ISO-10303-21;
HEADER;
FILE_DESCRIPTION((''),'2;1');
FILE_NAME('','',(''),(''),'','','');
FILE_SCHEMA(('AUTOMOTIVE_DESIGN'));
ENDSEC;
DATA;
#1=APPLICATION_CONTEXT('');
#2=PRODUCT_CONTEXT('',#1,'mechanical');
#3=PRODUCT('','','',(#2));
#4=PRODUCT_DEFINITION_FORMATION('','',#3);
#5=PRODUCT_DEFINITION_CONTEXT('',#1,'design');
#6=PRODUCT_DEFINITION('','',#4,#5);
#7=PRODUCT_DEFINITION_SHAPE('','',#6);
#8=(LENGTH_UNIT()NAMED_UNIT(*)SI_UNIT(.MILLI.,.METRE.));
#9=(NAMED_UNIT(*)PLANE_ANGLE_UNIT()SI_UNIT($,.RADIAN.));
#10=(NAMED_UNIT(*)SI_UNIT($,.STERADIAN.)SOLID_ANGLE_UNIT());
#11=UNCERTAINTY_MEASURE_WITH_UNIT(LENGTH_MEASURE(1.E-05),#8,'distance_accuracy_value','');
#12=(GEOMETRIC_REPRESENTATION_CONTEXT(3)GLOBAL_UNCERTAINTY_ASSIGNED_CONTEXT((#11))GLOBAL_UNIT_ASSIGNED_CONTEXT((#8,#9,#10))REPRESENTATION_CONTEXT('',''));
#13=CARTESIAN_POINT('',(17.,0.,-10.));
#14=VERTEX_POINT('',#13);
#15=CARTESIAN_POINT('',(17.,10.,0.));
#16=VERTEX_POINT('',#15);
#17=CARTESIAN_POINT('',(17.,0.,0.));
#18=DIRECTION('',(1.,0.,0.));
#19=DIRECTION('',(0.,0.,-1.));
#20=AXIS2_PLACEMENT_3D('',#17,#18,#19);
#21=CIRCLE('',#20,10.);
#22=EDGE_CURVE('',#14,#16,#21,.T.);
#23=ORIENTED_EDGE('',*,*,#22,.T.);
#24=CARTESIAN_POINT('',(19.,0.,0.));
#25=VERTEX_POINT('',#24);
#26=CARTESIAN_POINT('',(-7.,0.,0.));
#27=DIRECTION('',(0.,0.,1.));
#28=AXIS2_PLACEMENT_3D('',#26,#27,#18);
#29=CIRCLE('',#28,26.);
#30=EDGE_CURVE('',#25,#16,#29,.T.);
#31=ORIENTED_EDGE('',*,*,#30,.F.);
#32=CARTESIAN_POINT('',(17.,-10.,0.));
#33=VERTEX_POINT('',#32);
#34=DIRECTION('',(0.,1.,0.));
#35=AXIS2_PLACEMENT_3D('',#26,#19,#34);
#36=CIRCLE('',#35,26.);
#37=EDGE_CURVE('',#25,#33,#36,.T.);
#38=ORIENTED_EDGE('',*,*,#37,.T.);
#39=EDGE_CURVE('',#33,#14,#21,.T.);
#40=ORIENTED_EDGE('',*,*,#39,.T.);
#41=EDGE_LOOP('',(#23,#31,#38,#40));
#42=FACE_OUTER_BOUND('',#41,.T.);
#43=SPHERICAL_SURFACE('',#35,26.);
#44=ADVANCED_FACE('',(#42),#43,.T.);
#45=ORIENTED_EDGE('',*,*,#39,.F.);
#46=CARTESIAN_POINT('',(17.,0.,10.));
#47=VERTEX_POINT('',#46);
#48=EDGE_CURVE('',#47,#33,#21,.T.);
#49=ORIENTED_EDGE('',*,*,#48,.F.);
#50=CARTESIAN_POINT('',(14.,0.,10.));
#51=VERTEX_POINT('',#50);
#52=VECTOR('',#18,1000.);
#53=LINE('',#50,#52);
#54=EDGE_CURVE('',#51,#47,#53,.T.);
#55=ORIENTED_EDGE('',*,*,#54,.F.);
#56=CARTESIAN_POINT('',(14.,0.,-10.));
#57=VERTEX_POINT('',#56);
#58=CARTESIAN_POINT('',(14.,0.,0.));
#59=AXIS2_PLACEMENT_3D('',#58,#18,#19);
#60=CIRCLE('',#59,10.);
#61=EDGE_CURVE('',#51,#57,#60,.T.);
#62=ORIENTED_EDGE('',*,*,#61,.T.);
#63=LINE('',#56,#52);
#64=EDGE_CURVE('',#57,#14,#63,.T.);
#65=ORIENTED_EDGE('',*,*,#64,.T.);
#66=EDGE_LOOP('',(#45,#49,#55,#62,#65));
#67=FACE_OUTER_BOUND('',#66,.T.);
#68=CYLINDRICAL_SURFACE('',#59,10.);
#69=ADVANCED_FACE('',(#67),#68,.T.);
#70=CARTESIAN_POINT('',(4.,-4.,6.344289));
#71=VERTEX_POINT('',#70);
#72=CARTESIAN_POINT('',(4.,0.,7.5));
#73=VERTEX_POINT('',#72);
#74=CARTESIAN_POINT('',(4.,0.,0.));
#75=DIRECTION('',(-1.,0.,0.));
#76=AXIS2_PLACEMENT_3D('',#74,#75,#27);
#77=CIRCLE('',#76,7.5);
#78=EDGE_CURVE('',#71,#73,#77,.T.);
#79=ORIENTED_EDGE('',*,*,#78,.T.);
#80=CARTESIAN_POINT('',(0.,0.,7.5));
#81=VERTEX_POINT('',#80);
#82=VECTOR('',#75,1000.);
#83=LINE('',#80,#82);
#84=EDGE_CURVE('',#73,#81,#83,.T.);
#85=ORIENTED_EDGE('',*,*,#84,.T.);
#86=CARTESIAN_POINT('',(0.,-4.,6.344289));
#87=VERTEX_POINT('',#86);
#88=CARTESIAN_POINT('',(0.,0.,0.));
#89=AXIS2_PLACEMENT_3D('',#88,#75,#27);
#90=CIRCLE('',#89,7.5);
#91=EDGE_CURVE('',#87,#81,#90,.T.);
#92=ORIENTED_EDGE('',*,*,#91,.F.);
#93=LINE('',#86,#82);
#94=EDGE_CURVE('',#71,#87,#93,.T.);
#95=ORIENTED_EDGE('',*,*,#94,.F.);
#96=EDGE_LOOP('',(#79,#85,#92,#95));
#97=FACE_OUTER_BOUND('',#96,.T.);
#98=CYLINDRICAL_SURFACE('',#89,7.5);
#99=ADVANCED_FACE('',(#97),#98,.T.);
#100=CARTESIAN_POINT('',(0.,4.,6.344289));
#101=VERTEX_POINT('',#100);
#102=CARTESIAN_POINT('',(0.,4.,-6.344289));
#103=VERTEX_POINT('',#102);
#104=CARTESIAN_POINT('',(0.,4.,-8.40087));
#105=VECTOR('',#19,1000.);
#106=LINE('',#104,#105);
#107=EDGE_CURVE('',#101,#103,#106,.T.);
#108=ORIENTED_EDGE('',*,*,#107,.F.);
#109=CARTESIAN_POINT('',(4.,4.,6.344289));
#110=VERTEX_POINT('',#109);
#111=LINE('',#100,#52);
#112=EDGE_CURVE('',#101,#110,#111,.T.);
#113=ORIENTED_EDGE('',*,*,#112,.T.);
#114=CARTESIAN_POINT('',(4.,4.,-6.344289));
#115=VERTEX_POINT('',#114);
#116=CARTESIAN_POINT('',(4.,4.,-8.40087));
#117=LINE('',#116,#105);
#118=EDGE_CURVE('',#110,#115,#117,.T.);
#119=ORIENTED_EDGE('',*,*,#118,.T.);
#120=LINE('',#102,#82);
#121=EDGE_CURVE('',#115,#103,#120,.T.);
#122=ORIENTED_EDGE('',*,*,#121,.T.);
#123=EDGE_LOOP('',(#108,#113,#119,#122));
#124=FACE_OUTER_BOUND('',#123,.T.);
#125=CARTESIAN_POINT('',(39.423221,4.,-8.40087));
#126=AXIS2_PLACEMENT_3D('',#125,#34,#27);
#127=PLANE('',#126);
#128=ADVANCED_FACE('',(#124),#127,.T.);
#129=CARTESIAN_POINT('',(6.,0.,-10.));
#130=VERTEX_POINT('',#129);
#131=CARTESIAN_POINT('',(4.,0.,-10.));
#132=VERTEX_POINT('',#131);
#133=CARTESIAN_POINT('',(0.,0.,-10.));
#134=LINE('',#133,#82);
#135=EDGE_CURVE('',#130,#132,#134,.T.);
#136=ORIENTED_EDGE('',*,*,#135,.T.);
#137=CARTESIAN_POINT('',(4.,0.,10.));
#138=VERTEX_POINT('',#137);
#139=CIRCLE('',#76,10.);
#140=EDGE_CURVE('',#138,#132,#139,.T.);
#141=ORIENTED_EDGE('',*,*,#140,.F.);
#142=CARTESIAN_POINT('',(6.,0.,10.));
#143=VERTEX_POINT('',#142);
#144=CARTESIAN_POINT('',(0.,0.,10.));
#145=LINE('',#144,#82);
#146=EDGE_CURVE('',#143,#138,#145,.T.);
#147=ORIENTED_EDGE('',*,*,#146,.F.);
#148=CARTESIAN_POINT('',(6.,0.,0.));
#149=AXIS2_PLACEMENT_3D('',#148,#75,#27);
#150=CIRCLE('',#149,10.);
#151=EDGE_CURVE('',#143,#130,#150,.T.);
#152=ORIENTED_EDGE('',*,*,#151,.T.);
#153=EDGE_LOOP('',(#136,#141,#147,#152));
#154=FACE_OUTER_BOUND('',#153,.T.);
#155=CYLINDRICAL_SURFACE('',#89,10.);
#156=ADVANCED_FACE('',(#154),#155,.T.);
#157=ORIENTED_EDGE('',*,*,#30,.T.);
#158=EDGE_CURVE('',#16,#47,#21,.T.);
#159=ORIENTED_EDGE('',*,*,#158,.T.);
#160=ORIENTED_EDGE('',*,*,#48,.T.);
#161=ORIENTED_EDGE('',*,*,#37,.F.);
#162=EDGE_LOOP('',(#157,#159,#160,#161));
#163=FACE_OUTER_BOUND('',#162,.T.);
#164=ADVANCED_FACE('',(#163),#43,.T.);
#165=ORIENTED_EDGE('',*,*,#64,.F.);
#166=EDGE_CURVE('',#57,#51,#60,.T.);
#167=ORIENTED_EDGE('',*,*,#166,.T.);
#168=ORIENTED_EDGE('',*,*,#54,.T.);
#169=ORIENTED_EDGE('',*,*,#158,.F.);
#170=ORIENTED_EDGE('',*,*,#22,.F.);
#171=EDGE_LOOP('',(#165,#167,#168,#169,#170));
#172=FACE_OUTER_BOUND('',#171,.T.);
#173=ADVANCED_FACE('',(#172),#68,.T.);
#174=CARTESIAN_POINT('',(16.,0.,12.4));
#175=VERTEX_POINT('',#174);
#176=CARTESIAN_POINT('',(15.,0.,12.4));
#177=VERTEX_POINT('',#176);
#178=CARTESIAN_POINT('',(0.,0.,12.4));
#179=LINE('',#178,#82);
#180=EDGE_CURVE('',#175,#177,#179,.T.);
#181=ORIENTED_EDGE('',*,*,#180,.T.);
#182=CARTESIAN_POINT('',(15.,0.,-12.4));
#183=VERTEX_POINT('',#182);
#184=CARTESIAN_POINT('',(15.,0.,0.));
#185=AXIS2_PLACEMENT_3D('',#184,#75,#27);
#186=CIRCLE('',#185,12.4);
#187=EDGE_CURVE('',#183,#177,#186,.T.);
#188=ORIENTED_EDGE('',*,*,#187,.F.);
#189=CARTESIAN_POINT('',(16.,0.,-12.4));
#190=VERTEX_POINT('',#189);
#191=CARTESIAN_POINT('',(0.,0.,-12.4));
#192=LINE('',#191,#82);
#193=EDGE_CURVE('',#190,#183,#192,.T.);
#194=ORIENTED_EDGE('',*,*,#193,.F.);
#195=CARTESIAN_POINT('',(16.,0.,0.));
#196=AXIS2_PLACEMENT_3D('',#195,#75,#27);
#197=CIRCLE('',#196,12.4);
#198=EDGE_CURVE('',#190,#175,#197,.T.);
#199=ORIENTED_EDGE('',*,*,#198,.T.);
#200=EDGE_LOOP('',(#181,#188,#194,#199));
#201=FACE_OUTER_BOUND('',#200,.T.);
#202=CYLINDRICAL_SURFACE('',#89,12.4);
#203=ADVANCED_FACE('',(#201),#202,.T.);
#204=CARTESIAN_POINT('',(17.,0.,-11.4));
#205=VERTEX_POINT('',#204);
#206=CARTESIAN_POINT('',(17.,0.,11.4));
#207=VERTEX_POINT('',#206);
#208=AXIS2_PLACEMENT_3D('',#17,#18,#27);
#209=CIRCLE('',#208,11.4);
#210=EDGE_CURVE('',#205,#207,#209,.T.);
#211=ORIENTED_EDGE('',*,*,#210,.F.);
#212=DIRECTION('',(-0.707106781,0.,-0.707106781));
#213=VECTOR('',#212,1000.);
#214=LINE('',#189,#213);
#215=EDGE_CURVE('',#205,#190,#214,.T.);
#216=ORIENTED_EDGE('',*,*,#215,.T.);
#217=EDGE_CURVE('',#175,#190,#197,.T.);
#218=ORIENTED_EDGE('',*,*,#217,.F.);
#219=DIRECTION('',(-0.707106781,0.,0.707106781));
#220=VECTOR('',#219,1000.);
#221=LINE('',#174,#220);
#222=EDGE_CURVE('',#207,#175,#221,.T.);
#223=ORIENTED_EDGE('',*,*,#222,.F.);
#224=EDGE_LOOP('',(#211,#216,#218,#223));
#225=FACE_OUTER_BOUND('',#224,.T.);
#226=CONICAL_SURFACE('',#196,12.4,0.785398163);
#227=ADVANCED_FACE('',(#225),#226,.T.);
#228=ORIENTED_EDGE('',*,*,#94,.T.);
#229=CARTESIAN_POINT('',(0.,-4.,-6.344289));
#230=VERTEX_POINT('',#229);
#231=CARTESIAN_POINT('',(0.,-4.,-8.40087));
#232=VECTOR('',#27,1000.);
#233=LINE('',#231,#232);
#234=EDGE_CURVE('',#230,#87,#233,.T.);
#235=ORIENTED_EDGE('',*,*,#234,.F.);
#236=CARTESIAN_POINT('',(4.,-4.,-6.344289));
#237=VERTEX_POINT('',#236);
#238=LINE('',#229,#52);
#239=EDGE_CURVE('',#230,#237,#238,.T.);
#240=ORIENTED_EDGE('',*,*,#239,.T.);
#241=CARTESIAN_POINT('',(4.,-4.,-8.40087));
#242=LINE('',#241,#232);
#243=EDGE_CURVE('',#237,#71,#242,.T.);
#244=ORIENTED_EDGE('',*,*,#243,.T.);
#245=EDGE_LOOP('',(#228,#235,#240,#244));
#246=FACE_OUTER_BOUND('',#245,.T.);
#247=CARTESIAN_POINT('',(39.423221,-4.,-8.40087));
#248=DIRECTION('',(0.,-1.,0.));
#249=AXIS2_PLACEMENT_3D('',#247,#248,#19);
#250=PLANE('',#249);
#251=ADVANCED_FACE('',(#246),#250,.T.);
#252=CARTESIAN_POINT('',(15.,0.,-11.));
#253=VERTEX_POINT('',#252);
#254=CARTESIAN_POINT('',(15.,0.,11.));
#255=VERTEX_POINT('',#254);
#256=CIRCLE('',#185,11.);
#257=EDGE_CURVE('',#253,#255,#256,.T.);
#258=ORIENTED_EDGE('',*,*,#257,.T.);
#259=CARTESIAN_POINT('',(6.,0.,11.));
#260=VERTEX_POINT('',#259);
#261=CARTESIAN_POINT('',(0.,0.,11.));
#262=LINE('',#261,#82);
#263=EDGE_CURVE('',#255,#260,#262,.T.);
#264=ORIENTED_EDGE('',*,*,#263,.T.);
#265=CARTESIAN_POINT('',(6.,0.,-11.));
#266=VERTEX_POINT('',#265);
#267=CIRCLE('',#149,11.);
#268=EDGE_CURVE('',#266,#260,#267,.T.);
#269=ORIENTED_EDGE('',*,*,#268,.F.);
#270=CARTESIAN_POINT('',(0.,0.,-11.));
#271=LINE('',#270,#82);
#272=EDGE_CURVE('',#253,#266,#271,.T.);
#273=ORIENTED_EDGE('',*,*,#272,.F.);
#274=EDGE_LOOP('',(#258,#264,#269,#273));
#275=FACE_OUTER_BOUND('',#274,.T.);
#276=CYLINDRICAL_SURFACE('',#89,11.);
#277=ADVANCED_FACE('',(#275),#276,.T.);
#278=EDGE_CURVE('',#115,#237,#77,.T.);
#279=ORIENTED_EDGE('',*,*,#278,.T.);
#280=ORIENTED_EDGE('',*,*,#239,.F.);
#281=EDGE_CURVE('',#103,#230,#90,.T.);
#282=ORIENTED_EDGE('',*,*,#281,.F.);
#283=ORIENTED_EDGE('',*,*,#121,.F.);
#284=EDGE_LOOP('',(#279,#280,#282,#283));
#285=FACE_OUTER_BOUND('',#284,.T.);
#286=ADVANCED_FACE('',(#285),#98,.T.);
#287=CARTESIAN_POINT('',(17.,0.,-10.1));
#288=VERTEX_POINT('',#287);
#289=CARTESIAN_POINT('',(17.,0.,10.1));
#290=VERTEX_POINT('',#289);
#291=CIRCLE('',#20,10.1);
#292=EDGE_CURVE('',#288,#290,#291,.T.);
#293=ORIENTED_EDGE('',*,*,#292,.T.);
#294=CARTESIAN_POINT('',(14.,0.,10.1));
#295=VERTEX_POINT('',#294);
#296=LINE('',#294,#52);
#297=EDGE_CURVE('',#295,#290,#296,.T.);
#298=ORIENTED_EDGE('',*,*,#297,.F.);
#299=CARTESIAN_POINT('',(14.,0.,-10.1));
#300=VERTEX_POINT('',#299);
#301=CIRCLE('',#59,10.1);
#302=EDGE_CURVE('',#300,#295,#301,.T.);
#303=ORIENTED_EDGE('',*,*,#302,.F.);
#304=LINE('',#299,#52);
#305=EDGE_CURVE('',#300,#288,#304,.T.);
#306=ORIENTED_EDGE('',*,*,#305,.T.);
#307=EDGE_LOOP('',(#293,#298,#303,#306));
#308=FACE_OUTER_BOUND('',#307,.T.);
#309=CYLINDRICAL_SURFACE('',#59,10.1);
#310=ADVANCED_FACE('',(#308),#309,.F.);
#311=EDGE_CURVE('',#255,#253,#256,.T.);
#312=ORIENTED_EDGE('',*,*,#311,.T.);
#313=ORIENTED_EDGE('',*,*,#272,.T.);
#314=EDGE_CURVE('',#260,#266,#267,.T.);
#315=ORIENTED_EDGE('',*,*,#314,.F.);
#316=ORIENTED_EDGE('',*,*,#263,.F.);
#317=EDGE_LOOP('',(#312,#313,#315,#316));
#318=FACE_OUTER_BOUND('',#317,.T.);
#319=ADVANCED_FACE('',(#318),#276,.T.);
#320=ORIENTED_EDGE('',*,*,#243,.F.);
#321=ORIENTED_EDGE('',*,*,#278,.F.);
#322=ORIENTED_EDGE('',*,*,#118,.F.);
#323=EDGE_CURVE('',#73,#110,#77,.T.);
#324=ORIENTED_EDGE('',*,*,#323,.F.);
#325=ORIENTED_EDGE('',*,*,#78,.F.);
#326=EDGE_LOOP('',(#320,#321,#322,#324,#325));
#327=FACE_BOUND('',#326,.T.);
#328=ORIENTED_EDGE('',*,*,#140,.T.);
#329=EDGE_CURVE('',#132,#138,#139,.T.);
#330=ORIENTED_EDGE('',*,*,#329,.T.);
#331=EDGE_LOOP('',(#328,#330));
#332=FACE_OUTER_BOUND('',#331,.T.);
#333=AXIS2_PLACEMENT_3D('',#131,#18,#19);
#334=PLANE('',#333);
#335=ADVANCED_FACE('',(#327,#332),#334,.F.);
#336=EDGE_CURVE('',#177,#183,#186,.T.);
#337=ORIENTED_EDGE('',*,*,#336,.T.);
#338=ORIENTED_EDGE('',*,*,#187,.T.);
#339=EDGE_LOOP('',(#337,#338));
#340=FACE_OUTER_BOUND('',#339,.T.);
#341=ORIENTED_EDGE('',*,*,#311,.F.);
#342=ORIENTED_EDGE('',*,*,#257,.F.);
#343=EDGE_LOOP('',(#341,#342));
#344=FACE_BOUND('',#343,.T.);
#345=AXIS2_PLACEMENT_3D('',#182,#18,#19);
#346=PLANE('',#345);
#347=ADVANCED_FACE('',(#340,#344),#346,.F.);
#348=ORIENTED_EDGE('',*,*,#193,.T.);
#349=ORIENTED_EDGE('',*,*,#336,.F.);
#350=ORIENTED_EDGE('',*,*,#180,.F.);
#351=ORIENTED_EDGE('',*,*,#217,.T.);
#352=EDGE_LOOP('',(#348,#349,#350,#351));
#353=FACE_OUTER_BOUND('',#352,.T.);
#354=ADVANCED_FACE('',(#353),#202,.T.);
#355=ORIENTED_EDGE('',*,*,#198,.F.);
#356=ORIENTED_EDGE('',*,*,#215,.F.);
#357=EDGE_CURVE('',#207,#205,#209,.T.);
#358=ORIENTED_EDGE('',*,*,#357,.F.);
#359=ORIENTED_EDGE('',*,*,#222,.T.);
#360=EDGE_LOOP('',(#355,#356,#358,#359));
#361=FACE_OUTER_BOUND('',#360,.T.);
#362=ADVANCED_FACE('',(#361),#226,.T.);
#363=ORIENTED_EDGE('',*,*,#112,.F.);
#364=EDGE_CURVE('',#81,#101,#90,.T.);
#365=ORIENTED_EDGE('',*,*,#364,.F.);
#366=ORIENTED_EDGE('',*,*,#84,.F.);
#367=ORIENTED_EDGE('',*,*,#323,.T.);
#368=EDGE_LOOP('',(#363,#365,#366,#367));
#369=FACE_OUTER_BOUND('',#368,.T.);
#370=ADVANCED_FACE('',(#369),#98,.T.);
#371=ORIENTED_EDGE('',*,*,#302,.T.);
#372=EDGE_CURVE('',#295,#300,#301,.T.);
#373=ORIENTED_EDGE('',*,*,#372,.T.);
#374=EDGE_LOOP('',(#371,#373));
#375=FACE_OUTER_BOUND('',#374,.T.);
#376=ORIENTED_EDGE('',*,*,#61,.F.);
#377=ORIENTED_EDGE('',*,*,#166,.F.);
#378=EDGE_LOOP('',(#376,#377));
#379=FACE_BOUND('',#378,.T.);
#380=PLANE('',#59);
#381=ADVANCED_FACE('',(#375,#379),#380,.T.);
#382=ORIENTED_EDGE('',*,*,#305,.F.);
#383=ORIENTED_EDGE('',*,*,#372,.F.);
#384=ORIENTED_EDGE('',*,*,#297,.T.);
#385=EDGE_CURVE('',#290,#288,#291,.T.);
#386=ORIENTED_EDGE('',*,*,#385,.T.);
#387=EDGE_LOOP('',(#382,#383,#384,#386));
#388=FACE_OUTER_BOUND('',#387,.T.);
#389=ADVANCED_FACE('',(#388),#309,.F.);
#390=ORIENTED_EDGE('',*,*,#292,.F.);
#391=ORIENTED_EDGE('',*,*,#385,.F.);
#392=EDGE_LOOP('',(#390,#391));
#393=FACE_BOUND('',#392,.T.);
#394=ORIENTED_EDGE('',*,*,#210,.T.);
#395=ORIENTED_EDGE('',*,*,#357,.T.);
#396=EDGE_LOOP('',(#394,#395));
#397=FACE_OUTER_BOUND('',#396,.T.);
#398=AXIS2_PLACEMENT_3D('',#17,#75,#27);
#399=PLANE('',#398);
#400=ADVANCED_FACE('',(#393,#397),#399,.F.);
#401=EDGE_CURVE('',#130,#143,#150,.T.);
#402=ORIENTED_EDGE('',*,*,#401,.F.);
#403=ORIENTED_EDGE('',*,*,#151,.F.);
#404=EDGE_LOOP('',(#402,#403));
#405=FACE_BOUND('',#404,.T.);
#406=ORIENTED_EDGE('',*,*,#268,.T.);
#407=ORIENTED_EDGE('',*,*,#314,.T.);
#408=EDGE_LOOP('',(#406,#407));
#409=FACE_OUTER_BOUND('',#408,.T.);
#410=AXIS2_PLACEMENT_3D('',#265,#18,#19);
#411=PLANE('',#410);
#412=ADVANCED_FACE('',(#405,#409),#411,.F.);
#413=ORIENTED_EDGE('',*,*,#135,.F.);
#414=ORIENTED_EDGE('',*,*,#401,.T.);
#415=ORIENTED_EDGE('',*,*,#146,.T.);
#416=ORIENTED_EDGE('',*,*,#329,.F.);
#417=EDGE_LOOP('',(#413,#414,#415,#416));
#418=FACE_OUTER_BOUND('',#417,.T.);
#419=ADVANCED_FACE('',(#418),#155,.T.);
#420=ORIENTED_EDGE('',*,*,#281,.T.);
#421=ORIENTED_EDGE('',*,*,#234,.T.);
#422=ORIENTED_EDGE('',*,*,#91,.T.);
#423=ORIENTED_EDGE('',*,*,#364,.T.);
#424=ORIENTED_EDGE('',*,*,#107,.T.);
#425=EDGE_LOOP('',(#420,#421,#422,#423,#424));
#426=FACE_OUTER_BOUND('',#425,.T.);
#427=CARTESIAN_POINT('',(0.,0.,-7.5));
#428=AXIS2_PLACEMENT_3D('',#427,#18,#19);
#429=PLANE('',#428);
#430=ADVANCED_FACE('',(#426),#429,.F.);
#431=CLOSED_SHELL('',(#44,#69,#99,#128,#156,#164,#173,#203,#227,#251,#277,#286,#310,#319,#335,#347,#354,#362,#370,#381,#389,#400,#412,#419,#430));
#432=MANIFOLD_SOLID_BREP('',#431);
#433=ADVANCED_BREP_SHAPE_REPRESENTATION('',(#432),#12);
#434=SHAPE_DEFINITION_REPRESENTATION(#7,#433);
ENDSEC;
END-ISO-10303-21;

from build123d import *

# Parameters (mm, degrees)
CHAMFER1_SIZE       = 1
SKETCH5_OUTSIDE_W   = 34.778
SKETCH5_OUTSIDE_H   = 34.778
SKETCH5_OUTSIDE_W_2 = 16.801740482
SKETCH5_OUTSIDE_H_2 = 8
CUT_EXTRUDE2_DEPTH  = 4
CUT_EXTRUDE3_START  = -3
SKETCH7_R           = 10.1
SKETCH7_R_2         = 10
CUT_EXTRUDE3_DEPTH  = 3


with BuildPart() as part:
    # Sketch1 → Revolve1 (revolve)
    with BuildSketch(Plane(origin=(0, 0, 0), x_dir=(1, 0, 0), z_dir=(0, 1, 0)), mode=Mode.PRIVATE) as revolve1_sk:
        Polygon((0, 0), (17, 0), (17, 12.4), (15, 12.4), (15, 11), (6, 11), (6, 10), (4, 10), (4, 7.5), (0, 7.5), align=None)
    revolve(revolve1_sk.sketch.rotate(Axis((0, 0, 0), (1, 0, 0)), 180), axis=Axis((0, 0, 0), (1, 0, 0)))

    # Sketch3 → Revolve2 (revolve)
    with BuildSketch(Plane.XY):
        with BuildLine():
            Line((9, 0), (9, 10))
            Line((9, 10), (17, 10))
            ThreePointArc((17, 10), (18.495097568, 5.099019514), (19, 0))
            Line((19, 0), (9, 0))
        make_face()
    revolve(axis=Axis((9, 0, 0), (1, 0, 0)))

    # Chamfer1
    chamfer1_edges = [part.edges().sort_by_distance(p)[0] for p in [
        (17, 0, -12.4),
    ]]
    chamfer(chamfer1_edges, length=CHAMFER1_SIZE)

    # Sketch5 outside → Cut-Extrude2 (cut)
    with BuildSketch(Plane.ZY):
        Rectangle(SKETCH5_OUTSIDE_W, SKETCH5_OUTSIDE_H)
        Rectangle(SKETCH5_OUTSIDE_W_2, SKETCH5_OUTSIDE_H_2, mode=Mode.SUBTRACT)
    extrude(amount=-CUT_EXTRUDE2_DEPTH, mode=Mode.SUBTRACT)

    # Sketch7 → Cut-Extrude3 (cut)
    with BuildSketch(Plane(origin=(17, 0, 0), x_dir=(0, 0, -1), z_dir=(1, 0, 0)).offset(CUT_EXTRUDE3_START)):
        Circle(SKETCH7_R)
        with Locations(Location((0, 0, 0), (0, 0, 180))):
            Circle(SKETCH7_R_2, mode=Mode.SUBTRACT)
    extrude(amount=CUT_EXTRUDE3_DEPTH, mode=Mode.SUBTRACT)


solid = part.part
